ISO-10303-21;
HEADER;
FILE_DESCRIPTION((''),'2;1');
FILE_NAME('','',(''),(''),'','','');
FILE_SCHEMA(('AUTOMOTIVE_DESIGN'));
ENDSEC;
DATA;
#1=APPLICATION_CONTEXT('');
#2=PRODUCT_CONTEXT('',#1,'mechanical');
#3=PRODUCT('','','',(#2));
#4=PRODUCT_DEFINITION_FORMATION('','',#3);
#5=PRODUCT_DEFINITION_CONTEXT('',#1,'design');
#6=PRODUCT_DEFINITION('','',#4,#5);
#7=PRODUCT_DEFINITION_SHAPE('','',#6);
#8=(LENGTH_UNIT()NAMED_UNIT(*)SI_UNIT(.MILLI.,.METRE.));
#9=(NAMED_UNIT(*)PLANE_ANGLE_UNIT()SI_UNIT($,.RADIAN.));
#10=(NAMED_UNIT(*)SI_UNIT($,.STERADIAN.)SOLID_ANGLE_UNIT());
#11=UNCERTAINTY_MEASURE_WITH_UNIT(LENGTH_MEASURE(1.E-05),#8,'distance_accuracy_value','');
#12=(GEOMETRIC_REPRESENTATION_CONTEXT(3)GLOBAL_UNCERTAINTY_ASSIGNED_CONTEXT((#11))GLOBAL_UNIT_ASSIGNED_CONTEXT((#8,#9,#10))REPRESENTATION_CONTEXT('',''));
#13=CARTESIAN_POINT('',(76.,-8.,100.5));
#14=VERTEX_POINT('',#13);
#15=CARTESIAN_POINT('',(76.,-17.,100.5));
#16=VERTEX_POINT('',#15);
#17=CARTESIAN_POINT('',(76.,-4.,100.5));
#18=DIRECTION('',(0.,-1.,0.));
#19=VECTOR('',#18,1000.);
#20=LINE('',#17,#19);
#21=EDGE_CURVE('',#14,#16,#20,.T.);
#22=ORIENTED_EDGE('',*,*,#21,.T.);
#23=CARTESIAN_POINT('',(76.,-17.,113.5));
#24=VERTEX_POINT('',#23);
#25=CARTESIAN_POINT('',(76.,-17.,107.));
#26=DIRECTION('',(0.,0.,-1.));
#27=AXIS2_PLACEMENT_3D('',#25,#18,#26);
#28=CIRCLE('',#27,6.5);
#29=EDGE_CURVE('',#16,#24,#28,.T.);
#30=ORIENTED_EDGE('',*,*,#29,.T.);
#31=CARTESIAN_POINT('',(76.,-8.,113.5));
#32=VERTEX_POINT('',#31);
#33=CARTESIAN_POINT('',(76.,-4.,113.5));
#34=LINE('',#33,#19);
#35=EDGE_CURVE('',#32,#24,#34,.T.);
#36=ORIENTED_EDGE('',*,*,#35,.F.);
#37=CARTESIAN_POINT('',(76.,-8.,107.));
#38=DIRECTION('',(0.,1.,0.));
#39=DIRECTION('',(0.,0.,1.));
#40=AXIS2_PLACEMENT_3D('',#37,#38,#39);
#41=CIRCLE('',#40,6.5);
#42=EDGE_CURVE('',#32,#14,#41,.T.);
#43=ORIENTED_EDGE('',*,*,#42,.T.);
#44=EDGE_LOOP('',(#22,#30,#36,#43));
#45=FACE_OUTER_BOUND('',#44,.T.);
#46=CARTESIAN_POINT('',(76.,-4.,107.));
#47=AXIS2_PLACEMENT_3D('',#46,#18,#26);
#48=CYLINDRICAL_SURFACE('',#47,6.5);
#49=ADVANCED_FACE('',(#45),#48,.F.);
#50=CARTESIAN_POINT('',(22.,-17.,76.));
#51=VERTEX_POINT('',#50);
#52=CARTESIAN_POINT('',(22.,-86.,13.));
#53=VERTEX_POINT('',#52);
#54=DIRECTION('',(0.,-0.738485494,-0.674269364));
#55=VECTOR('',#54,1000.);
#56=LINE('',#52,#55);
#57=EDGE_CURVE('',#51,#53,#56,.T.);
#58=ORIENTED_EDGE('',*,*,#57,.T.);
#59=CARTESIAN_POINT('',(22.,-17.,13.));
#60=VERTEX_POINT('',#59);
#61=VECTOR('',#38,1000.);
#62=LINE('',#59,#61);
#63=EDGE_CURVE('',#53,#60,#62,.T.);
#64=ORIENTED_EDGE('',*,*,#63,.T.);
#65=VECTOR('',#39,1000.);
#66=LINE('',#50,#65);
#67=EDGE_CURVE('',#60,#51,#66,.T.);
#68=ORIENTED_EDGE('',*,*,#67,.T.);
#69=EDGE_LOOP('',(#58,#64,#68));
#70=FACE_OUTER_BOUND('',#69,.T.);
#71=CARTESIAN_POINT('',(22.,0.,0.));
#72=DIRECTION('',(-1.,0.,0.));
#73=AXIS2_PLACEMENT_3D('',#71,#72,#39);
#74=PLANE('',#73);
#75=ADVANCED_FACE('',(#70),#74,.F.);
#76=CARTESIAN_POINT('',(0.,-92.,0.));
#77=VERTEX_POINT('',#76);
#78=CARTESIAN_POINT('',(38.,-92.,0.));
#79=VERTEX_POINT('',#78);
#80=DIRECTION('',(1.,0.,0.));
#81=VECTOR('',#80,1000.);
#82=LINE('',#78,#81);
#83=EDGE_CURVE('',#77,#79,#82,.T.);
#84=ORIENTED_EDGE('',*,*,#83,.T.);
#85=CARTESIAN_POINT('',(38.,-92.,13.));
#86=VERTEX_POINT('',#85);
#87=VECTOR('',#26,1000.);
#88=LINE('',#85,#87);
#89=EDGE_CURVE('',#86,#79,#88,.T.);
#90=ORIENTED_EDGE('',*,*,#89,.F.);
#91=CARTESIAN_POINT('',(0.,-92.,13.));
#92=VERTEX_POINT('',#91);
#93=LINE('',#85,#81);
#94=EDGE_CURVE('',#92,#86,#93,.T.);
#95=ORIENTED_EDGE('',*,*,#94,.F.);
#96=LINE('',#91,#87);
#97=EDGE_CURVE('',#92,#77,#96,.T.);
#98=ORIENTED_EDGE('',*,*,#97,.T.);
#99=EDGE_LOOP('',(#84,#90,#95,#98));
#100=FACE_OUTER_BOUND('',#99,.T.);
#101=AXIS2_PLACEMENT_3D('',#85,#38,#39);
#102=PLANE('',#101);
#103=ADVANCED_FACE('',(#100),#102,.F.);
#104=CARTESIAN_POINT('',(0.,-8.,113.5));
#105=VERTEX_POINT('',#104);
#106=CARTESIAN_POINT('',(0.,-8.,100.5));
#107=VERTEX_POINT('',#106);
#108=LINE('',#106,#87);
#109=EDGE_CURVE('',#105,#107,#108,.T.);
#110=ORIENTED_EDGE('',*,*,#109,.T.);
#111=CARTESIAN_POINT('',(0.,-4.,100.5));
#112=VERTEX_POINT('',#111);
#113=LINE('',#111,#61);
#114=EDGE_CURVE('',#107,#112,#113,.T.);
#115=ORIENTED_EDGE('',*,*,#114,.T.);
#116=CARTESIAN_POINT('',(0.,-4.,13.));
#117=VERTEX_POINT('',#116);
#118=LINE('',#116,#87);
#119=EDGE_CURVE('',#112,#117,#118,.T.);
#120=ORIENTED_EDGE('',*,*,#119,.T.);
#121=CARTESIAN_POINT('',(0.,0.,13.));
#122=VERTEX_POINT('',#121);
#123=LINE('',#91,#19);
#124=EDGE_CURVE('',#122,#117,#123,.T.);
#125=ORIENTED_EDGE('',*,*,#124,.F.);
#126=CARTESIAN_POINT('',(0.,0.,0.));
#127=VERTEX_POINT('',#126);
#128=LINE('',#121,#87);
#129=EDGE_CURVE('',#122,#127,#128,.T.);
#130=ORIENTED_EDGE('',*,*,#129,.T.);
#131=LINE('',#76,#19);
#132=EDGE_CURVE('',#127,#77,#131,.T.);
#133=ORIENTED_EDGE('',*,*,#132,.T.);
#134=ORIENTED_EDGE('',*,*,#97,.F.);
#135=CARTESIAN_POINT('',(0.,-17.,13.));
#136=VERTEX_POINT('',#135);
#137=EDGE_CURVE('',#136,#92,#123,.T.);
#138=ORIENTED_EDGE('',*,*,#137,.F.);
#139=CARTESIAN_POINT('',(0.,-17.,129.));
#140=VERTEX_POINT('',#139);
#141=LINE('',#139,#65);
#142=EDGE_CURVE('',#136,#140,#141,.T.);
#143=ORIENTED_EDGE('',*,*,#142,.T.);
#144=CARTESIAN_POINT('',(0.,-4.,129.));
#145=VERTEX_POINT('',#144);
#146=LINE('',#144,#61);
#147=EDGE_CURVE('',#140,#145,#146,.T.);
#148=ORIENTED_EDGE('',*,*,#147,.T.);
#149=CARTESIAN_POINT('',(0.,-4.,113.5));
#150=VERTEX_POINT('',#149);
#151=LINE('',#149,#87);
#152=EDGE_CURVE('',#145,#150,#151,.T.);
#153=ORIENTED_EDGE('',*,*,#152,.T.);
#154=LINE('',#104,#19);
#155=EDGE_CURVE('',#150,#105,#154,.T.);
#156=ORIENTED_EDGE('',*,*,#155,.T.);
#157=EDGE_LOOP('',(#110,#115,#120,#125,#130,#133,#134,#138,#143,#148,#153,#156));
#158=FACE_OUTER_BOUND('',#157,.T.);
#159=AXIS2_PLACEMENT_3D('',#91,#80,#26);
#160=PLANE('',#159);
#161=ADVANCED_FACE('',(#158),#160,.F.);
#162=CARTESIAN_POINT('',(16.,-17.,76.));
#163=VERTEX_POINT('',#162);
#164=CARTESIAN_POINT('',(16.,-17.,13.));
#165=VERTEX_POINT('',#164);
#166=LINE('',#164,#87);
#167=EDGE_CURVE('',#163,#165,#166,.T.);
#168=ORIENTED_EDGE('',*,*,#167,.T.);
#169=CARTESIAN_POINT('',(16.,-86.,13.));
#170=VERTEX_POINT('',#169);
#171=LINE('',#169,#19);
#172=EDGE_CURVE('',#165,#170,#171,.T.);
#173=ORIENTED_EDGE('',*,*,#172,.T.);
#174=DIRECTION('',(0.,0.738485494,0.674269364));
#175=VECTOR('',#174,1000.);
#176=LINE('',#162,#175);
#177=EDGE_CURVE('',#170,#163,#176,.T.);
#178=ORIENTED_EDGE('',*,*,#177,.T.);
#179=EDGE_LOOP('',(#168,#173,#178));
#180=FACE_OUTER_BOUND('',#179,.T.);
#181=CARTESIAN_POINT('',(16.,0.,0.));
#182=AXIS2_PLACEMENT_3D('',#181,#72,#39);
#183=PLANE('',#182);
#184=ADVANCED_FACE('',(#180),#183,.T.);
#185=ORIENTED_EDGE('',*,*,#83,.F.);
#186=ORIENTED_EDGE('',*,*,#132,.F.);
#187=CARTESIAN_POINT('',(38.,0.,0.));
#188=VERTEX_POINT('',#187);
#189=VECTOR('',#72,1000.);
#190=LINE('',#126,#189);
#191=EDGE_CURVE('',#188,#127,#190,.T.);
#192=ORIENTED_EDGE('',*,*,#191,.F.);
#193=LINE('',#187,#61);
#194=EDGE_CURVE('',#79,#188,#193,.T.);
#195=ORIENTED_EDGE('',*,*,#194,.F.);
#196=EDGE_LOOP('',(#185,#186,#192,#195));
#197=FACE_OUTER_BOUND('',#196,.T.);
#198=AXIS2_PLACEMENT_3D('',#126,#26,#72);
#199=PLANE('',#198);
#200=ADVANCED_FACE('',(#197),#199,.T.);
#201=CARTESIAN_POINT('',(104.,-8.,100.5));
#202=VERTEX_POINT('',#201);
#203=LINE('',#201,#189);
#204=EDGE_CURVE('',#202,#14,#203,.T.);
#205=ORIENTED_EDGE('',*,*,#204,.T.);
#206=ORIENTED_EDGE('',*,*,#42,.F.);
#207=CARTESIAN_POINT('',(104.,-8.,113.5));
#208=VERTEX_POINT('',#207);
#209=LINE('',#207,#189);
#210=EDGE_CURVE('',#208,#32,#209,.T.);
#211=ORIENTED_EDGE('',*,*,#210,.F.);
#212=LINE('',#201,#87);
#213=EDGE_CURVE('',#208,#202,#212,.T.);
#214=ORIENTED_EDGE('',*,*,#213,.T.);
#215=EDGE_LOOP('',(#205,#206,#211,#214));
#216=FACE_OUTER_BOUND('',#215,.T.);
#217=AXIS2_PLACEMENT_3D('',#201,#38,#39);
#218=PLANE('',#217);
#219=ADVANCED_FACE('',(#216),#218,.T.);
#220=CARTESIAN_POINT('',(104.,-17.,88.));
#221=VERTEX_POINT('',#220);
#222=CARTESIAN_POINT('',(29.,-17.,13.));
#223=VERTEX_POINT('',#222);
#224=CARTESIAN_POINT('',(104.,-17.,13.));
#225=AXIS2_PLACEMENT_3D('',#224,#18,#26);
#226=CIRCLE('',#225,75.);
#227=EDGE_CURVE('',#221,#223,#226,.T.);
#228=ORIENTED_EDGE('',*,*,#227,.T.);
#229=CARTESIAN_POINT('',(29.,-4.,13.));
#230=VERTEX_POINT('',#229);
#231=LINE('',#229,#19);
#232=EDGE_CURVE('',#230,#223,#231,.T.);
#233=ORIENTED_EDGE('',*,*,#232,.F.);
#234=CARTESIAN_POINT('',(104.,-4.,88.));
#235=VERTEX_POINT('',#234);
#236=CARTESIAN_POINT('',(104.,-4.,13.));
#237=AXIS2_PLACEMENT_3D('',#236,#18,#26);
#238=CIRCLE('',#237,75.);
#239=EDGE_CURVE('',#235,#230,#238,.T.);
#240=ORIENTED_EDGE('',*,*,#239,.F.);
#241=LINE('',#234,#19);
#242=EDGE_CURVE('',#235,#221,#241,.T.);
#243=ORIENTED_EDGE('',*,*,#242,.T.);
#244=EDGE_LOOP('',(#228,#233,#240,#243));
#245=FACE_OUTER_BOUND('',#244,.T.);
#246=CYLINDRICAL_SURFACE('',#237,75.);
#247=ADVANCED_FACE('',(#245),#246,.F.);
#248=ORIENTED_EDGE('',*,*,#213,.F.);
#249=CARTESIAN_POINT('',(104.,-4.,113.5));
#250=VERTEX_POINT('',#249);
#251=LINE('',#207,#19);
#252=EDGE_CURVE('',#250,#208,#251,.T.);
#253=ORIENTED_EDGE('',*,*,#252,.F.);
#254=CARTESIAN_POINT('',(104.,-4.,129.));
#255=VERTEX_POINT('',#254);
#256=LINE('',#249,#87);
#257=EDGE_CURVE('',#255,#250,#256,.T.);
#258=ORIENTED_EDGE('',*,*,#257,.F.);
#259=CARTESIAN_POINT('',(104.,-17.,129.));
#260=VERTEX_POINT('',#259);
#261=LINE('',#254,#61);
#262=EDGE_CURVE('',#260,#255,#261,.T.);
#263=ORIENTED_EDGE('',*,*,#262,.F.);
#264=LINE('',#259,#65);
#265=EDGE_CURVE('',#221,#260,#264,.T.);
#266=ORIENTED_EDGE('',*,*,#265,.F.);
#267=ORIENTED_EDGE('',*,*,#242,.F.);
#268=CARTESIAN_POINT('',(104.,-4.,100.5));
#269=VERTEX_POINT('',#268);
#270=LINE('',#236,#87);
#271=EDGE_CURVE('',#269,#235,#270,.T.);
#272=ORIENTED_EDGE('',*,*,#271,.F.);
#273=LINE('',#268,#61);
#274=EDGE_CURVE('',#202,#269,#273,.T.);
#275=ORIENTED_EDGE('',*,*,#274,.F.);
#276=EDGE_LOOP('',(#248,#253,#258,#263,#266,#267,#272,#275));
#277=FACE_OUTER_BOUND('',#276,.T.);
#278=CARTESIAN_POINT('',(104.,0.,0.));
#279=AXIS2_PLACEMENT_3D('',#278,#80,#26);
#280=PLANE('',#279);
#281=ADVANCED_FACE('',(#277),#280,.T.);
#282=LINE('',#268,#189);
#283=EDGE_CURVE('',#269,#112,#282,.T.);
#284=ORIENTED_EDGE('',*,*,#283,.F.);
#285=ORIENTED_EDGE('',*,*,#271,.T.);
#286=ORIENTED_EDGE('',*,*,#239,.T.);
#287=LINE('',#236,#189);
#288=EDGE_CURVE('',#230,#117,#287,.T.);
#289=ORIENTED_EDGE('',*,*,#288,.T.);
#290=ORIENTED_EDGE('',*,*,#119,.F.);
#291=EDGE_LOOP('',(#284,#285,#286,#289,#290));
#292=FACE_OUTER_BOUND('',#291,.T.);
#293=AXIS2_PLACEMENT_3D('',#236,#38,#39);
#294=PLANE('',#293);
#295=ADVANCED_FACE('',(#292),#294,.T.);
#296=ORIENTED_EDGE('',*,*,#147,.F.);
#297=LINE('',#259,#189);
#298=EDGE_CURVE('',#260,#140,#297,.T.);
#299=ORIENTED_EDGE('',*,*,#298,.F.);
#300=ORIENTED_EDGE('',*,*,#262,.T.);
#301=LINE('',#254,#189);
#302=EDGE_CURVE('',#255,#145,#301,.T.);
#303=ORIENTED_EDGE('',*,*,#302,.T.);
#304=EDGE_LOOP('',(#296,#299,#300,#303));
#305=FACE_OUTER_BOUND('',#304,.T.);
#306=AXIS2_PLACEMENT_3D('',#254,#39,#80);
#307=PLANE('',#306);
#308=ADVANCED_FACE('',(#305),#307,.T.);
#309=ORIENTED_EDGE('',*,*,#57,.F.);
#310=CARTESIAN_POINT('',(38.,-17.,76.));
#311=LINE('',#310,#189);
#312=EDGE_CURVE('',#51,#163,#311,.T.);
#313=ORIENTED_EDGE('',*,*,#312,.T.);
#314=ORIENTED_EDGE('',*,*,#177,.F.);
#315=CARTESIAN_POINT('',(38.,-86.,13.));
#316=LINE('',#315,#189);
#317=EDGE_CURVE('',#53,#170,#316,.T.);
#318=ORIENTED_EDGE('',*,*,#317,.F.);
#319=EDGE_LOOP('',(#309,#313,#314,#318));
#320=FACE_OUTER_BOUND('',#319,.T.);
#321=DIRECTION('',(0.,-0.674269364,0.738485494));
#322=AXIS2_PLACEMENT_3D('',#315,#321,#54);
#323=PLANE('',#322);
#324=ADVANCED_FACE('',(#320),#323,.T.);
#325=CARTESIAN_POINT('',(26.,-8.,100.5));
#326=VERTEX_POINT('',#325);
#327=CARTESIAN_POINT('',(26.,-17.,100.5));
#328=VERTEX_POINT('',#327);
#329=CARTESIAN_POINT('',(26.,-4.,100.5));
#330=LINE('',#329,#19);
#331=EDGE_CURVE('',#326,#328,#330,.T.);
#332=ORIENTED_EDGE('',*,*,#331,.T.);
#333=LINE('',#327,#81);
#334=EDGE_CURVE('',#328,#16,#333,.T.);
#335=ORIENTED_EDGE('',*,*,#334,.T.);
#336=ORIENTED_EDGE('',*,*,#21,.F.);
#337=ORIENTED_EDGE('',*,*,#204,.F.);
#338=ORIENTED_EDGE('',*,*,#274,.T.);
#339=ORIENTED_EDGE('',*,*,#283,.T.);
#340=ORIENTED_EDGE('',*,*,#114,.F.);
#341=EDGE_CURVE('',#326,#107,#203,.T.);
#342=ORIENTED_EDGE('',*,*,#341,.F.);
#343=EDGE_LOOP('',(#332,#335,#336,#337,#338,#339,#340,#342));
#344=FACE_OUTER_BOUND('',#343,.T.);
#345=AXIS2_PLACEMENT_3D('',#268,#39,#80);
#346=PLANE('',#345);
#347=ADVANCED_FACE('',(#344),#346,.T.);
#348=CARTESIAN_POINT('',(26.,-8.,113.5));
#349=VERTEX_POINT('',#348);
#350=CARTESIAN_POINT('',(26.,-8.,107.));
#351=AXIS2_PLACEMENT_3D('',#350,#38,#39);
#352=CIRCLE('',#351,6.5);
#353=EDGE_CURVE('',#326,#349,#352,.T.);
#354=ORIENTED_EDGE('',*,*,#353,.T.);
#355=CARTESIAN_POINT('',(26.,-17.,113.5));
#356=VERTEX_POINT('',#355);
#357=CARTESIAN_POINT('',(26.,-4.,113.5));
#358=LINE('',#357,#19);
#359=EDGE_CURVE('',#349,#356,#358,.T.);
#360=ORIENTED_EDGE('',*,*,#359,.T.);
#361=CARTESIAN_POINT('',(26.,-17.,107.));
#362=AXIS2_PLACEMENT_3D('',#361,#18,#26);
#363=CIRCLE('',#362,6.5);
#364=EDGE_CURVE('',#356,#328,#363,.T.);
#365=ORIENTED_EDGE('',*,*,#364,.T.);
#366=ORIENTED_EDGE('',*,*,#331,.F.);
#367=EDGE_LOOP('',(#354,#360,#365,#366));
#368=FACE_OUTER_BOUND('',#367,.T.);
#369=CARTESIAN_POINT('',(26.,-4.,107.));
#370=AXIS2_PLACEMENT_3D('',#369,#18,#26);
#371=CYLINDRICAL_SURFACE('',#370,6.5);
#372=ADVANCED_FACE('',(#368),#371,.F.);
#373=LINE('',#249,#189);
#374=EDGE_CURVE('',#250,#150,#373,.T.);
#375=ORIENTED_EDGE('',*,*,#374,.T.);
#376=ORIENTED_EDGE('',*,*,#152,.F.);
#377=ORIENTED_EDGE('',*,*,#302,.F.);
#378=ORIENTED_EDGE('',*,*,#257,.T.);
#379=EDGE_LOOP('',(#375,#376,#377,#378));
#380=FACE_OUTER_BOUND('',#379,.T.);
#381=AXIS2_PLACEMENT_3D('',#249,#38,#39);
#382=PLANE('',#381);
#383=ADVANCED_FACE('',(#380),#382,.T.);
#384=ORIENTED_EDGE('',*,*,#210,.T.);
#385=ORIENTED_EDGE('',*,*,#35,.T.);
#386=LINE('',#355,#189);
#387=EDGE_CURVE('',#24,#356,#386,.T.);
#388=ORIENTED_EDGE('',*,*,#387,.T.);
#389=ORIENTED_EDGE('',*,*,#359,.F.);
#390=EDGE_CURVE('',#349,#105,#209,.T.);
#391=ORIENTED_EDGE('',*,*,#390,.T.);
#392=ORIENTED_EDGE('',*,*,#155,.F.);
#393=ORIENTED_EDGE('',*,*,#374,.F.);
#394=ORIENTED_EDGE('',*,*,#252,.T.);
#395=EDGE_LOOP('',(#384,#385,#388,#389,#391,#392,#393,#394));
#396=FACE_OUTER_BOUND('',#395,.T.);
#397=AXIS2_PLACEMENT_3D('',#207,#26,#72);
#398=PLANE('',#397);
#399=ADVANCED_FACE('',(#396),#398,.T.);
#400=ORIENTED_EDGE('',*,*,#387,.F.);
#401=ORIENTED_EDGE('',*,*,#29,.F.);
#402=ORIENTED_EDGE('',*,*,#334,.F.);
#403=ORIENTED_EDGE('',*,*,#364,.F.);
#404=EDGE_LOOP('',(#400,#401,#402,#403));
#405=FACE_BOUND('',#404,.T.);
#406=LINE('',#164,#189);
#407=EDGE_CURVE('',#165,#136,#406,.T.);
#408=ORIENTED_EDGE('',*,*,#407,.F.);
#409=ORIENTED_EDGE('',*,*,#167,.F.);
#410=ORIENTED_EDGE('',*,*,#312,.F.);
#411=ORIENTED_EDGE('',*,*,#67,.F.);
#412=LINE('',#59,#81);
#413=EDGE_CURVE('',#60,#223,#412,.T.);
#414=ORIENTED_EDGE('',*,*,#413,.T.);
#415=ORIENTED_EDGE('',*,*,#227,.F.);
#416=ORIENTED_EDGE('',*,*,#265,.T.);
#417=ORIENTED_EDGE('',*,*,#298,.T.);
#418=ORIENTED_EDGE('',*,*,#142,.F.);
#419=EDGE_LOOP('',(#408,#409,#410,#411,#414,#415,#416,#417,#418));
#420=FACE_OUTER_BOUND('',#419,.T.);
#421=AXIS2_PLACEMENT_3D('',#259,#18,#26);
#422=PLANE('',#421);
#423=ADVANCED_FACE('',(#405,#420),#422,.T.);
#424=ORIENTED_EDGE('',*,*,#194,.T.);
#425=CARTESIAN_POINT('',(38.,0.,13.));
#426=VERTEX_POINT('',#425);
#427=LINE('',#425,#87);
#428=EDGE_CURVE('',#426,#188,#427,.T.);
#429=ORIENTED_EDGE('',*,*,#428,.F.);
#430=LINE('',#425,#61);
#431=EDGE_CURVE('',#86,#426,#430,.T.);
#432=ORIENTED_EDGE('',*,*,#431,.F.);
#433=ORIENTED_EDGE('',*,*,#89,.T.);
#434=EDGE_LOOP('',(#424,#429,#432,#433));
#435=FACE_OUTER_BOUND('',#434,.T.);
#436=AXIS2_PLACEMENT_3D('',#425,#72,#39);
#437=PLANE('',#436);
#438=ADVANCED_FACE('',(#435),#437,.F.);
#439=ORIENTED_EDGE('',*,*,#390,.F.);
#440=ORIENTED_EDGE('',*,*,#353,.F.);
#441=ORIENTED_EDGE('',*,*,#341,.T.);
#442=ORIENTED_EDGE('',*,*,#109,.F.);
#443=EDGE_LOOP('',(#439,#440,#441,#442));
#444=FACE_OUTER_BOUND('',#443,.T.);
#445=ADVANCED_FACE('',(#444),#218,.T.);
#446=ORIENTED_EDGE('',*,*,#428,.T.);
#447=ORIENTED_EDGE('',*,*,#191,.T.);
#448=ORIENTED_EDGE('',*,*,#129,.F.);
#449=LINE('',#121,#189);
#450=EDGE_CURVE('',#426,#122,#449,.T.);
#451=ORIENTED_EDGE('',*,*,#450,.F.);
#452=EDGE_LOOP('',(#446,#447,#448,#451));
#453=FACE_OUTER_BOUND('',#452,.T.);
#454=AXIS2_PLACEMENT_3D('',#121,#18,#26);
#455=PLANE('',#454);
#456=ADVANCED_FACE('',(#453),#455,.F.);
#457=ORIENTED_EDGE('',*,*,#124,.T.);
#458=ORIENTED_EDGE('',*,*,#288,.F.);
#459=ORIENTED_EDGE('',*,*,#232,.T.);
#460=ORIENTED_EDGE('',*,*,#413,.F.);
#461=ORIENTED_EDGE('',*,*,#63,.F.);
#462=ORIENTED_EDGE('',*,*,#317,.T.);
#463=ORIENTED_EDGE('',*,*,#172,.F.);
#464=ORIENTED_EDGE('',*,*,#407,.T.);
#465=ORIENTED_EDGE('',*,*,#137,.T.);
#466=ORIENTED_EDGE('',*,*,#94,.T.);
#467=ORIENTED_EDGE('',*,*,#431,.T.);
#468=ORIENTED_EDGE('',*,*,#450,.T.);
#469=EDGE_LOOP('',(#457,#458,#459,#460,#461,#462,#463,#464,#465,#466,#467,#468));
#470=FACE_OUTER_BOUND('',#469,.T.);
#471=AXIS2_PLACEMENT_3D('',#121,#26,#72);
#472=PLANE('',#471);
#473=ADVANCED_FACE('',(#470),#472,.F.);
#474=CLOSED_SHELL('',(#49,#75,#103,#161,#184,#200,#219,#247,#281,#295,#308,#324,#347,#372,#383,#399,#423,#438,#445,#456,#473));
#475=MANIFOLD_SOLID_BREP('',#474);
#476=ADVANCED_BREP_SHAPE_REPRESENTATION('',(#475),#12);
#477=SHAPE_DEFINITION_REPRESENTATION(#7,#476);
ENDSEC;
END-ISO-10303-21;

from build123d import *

# Parameters (mm, degrees)
BASE_PLATE_SKETCH_W     = 38
BASE_PLATE_SKETCH_H     = 92
BASE_PLATE_DEPTH        = 13
MAIN_BODY_104MM_DEPTH   = 104
CURVED_RELIEF_CUT_DEPTH = 13
SLOT_CUT_DEPTH          = 13
GUSSET_BOSS_38MM_DEPTH  = 38
NOTCH_CUT_A_DEPTH       = 16
NOTCH_CUT_B_DEPTH       = 16


with BuildPart() as part:
    # Base Plate Sketch → Base Plate (new body)
    with BuildSketch(Plane.XY):
        with Locations((19, -46)):
            Rectangle(BASE_PLATE_SKETCH_W, BASE_PLATE_SKETCH_H)
    extrude(amount=BASE_PLATE_DEPTH)

    # Main Body Profile Sketch → Main Body 104mm (add)
    with BuildSketch(Plane.ZY):
        Polygon((13, -4), (100.5, -4), (100.5, -8), (113.5, -8), (113.5, -4), (129, -4), (129, -17), (13, -17), align=None)
    extrude(amount=-MAIN_BODY_104MM_DEPTH)

    # Curved Relief Sketch → Curved Relief Cut (cut)
    with BuildSketch(Plane.XZ.offset(17)):
        with BuildLine():
            Line((104, 88), (104, 13))
            Line((104, 13), (29, 13))
            ThreePointArc((29, 13), (50.966991411, 66.033008589), (104, 88))
        make_face()
    extrude(amount=-CURVED_RELIEF_CUT_DEPTH, mode=Mode.SUBTRACT)

    # Slot Sketch → Slot Cut (cut)
    with BuildSketch(Plane.XZ.offset(17)):
        with BuildLine():
            Line((26, 113.5), (76, 113.5))
            ThreePointArc((76, 113.5), (82.5, 107), (76, 100.5))
            Line((76, 100.5), (26, 100.5))
            ThreePointArc((26, 100.5), (19.5, 107), (26, 113.5))
        make_face()
    extrude(amount=-SLOT_CUT_DEPTH, mode=Mode.SUBTRACT)

    # Gusset Boss Sketch → Gusset Boss 38mm (add)
    with BuildSketch(Plane.ZY):
        Polygon((13, -17), (76, -17), (13, -86), align=None)
    extrude(amount=-GUSSET_BOSS_38MM_DEPTH)

    # Notch Cut A Sketch → Notch Cut A (cut)
    with BuildSketch(Plane(origin=(38, 0, 0), x_dir=(0, 0, -1), z_dir=(1, 0, 0))):
        Polygon((-76, -17), (-13, -17), (-13, -86), align=None)
    extrude(amount=-NOTCH_CUT_A_DEPTH, mode=Mode.SUBTRACT)

    # Notch Cut B Sketch → Notch Cut B (cut)
    with BuildSketch(Plane.ZY):
        Polygon((76, -17), (13, -86), (13, -17), align=None)
    extrude(amount=-NOTCH_CUT_B_DEPTH, mode=Mode.SUBTRACT)


solid = part.part
